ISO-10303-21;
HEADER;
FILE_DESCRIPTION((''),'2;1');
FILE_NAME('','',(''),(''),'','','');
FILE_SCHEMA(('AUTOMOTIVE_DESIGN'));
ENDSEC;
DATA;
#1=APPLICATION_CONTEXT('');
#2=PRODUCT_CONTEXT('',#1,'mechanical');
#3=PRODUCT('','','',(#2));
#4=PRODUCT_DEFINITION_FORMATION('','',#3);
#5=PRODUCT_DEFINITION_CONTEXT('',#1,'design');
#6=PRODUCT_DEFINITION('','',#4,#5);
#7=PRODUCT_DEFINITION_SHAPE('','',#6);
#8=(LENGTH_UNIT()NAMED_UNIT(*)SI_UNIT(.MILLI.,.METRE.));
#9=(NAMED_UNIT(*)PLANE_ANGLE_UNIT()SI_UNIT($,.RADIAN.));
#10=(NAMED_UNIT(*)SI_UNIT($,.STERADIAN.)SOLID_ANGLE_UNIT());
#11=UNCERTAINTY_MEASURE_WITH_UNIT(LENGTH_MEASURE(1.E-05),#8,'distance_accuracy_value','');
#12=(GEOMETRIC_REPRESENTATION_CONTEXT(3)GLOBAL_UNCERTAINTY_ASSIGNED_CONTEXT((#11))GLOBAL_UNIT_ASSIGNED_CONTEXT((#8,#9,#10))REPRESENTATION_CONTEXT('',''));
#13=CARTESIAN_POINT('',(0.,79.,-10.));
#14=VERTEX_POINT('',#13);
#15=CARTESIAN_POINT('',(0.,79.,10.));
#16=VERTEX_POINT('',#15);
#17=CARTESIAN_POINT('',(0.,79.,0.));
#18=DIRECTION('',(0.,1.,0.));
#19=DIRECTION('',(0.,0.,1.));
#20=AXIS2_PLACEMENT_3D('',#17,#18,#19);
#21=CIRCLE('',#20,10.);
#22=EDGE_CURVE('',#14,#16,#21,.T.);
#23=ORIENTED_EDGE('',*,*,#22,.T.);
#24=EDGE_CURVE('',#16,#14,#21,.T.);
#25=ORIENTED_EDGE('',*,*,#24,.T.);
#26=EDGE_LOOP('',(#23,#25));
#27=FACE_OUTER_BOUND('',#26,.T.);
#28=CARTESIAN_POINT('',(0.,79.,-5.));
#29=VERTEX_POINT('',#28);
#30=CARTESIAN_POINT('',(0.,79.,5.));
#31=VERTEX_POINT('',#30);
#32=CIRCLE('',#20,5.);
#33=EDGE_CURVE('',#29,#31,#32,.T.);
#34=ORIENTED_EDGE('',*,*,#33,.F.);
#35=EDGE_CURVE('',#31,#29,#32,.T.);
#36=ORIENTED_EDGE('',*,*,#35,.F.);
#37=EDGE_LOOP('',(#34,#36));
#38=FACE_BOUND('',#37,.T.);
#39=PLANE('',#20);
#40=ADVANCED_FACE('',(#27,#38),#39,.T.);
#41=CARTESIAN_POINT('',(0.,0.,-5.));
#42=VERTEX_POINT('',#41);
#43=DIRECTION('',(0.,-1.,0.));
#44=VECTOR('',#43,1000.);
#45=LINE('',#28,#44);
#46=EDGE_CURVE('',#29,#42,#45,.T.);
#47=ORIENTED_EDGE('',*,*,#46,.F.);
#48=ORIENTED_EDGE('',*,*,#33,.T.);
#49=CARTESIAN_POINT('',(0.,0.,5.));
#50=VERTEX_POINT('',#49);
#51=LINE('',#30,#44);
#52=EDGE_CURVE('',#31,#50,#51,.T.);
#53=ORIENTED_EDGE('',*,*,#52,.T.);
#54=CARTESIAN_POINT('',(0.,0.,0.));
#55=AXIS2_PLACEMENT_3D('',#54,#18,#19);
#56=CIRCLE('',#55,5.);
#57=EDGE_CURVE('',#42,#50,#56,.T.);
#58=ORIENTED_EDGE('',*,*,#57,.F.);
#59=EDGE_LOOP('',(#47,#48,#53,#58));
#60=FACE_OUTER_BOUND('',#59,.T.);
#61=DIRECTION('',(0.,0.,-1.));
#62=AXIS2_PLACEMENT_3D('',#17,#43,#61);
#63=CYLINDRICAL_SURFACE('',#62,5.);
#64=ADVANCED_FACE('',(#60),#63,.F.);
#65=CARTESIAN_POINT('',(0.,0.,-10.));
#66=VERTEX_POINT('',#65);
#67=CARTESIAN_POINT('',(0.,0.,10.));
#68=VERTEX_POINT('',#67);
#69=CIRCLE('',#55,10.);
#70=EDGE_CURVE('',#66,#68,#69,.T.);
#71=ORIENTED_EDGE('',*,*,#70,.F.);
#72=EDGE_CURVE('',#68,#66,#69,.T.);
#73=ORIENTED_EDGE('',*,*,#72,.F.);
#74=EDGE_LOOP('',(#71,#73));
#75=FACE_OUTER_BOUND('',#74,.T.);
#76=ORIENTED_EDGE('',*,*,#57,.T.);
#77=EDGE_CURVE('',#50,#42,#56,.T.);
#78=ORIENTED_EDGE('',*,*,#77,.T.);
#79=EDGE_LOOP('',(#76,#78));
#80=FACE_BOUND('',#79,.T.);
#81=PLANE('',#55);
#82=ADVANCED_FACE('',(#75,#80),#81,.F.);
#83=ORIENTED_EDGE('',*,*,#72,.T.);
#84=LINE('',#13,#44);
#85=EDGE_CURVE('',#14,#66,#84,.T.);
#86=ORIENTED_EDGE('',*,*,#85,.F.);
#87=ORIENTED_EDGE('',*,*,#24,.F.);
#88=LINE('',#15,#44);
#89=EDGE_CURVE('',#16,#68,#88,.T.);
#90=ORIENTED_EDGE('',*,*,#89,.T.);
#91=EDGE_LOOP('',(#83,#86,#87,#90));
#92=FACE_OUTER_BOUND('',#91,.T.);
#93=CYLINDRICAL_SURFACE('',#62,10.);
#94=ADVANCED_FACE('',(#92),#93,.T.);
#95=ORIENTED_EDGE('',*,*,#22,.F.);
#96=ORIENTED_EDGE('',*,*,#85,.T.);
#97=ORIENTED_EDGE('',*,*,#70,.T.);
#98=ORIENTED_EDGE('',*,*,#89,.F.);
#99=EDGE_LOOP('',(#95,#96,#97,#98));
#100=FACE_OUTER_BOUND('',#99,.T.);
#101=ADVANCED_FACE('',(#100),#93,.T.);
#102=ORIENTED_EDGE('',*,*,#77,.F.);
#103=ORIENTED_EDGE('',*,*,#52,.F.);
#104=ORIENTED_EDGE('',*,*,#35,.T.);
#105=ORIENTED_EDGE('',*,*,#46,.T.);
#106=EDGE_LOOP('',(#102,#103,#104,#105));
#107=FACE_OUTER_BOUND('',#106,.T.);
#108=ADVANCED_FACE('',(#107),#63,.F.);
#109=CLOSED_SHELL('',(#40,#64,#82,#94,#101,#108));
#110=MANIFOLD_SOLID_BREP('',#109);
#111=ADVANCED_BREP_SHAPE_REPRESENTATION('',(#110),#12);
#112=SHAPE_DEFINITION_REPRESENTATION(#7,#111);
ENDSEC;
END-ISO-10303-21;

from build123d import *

# Parameters (mm, degrees)
SKETCH1_R           = 10
SKETCH1_R_2         = 5
BOSS_EXTRUDE1_DEPTH = 79


with BuildPart() as part:
    # Sketch1 → Boss-Extrude1 (new body)
    with BuildSketch(Plane(origin=(0, 0, 0), x_dir=(1, 0, 0), z_dir=(0, 1, 0))):
        with Locations(Location((0, 0, 0), (0, 0, 270))):
            Circle(SKETCH1_R)
        with Locations(Location((0, 0, 0), (0, 0, 270))):
            Circle(SKETCH1_R_2, mode=Mode.SUBTRACT)
    extrude(amount=BOSS_EXTRUDE1_DEPTH)


solid = part.part
